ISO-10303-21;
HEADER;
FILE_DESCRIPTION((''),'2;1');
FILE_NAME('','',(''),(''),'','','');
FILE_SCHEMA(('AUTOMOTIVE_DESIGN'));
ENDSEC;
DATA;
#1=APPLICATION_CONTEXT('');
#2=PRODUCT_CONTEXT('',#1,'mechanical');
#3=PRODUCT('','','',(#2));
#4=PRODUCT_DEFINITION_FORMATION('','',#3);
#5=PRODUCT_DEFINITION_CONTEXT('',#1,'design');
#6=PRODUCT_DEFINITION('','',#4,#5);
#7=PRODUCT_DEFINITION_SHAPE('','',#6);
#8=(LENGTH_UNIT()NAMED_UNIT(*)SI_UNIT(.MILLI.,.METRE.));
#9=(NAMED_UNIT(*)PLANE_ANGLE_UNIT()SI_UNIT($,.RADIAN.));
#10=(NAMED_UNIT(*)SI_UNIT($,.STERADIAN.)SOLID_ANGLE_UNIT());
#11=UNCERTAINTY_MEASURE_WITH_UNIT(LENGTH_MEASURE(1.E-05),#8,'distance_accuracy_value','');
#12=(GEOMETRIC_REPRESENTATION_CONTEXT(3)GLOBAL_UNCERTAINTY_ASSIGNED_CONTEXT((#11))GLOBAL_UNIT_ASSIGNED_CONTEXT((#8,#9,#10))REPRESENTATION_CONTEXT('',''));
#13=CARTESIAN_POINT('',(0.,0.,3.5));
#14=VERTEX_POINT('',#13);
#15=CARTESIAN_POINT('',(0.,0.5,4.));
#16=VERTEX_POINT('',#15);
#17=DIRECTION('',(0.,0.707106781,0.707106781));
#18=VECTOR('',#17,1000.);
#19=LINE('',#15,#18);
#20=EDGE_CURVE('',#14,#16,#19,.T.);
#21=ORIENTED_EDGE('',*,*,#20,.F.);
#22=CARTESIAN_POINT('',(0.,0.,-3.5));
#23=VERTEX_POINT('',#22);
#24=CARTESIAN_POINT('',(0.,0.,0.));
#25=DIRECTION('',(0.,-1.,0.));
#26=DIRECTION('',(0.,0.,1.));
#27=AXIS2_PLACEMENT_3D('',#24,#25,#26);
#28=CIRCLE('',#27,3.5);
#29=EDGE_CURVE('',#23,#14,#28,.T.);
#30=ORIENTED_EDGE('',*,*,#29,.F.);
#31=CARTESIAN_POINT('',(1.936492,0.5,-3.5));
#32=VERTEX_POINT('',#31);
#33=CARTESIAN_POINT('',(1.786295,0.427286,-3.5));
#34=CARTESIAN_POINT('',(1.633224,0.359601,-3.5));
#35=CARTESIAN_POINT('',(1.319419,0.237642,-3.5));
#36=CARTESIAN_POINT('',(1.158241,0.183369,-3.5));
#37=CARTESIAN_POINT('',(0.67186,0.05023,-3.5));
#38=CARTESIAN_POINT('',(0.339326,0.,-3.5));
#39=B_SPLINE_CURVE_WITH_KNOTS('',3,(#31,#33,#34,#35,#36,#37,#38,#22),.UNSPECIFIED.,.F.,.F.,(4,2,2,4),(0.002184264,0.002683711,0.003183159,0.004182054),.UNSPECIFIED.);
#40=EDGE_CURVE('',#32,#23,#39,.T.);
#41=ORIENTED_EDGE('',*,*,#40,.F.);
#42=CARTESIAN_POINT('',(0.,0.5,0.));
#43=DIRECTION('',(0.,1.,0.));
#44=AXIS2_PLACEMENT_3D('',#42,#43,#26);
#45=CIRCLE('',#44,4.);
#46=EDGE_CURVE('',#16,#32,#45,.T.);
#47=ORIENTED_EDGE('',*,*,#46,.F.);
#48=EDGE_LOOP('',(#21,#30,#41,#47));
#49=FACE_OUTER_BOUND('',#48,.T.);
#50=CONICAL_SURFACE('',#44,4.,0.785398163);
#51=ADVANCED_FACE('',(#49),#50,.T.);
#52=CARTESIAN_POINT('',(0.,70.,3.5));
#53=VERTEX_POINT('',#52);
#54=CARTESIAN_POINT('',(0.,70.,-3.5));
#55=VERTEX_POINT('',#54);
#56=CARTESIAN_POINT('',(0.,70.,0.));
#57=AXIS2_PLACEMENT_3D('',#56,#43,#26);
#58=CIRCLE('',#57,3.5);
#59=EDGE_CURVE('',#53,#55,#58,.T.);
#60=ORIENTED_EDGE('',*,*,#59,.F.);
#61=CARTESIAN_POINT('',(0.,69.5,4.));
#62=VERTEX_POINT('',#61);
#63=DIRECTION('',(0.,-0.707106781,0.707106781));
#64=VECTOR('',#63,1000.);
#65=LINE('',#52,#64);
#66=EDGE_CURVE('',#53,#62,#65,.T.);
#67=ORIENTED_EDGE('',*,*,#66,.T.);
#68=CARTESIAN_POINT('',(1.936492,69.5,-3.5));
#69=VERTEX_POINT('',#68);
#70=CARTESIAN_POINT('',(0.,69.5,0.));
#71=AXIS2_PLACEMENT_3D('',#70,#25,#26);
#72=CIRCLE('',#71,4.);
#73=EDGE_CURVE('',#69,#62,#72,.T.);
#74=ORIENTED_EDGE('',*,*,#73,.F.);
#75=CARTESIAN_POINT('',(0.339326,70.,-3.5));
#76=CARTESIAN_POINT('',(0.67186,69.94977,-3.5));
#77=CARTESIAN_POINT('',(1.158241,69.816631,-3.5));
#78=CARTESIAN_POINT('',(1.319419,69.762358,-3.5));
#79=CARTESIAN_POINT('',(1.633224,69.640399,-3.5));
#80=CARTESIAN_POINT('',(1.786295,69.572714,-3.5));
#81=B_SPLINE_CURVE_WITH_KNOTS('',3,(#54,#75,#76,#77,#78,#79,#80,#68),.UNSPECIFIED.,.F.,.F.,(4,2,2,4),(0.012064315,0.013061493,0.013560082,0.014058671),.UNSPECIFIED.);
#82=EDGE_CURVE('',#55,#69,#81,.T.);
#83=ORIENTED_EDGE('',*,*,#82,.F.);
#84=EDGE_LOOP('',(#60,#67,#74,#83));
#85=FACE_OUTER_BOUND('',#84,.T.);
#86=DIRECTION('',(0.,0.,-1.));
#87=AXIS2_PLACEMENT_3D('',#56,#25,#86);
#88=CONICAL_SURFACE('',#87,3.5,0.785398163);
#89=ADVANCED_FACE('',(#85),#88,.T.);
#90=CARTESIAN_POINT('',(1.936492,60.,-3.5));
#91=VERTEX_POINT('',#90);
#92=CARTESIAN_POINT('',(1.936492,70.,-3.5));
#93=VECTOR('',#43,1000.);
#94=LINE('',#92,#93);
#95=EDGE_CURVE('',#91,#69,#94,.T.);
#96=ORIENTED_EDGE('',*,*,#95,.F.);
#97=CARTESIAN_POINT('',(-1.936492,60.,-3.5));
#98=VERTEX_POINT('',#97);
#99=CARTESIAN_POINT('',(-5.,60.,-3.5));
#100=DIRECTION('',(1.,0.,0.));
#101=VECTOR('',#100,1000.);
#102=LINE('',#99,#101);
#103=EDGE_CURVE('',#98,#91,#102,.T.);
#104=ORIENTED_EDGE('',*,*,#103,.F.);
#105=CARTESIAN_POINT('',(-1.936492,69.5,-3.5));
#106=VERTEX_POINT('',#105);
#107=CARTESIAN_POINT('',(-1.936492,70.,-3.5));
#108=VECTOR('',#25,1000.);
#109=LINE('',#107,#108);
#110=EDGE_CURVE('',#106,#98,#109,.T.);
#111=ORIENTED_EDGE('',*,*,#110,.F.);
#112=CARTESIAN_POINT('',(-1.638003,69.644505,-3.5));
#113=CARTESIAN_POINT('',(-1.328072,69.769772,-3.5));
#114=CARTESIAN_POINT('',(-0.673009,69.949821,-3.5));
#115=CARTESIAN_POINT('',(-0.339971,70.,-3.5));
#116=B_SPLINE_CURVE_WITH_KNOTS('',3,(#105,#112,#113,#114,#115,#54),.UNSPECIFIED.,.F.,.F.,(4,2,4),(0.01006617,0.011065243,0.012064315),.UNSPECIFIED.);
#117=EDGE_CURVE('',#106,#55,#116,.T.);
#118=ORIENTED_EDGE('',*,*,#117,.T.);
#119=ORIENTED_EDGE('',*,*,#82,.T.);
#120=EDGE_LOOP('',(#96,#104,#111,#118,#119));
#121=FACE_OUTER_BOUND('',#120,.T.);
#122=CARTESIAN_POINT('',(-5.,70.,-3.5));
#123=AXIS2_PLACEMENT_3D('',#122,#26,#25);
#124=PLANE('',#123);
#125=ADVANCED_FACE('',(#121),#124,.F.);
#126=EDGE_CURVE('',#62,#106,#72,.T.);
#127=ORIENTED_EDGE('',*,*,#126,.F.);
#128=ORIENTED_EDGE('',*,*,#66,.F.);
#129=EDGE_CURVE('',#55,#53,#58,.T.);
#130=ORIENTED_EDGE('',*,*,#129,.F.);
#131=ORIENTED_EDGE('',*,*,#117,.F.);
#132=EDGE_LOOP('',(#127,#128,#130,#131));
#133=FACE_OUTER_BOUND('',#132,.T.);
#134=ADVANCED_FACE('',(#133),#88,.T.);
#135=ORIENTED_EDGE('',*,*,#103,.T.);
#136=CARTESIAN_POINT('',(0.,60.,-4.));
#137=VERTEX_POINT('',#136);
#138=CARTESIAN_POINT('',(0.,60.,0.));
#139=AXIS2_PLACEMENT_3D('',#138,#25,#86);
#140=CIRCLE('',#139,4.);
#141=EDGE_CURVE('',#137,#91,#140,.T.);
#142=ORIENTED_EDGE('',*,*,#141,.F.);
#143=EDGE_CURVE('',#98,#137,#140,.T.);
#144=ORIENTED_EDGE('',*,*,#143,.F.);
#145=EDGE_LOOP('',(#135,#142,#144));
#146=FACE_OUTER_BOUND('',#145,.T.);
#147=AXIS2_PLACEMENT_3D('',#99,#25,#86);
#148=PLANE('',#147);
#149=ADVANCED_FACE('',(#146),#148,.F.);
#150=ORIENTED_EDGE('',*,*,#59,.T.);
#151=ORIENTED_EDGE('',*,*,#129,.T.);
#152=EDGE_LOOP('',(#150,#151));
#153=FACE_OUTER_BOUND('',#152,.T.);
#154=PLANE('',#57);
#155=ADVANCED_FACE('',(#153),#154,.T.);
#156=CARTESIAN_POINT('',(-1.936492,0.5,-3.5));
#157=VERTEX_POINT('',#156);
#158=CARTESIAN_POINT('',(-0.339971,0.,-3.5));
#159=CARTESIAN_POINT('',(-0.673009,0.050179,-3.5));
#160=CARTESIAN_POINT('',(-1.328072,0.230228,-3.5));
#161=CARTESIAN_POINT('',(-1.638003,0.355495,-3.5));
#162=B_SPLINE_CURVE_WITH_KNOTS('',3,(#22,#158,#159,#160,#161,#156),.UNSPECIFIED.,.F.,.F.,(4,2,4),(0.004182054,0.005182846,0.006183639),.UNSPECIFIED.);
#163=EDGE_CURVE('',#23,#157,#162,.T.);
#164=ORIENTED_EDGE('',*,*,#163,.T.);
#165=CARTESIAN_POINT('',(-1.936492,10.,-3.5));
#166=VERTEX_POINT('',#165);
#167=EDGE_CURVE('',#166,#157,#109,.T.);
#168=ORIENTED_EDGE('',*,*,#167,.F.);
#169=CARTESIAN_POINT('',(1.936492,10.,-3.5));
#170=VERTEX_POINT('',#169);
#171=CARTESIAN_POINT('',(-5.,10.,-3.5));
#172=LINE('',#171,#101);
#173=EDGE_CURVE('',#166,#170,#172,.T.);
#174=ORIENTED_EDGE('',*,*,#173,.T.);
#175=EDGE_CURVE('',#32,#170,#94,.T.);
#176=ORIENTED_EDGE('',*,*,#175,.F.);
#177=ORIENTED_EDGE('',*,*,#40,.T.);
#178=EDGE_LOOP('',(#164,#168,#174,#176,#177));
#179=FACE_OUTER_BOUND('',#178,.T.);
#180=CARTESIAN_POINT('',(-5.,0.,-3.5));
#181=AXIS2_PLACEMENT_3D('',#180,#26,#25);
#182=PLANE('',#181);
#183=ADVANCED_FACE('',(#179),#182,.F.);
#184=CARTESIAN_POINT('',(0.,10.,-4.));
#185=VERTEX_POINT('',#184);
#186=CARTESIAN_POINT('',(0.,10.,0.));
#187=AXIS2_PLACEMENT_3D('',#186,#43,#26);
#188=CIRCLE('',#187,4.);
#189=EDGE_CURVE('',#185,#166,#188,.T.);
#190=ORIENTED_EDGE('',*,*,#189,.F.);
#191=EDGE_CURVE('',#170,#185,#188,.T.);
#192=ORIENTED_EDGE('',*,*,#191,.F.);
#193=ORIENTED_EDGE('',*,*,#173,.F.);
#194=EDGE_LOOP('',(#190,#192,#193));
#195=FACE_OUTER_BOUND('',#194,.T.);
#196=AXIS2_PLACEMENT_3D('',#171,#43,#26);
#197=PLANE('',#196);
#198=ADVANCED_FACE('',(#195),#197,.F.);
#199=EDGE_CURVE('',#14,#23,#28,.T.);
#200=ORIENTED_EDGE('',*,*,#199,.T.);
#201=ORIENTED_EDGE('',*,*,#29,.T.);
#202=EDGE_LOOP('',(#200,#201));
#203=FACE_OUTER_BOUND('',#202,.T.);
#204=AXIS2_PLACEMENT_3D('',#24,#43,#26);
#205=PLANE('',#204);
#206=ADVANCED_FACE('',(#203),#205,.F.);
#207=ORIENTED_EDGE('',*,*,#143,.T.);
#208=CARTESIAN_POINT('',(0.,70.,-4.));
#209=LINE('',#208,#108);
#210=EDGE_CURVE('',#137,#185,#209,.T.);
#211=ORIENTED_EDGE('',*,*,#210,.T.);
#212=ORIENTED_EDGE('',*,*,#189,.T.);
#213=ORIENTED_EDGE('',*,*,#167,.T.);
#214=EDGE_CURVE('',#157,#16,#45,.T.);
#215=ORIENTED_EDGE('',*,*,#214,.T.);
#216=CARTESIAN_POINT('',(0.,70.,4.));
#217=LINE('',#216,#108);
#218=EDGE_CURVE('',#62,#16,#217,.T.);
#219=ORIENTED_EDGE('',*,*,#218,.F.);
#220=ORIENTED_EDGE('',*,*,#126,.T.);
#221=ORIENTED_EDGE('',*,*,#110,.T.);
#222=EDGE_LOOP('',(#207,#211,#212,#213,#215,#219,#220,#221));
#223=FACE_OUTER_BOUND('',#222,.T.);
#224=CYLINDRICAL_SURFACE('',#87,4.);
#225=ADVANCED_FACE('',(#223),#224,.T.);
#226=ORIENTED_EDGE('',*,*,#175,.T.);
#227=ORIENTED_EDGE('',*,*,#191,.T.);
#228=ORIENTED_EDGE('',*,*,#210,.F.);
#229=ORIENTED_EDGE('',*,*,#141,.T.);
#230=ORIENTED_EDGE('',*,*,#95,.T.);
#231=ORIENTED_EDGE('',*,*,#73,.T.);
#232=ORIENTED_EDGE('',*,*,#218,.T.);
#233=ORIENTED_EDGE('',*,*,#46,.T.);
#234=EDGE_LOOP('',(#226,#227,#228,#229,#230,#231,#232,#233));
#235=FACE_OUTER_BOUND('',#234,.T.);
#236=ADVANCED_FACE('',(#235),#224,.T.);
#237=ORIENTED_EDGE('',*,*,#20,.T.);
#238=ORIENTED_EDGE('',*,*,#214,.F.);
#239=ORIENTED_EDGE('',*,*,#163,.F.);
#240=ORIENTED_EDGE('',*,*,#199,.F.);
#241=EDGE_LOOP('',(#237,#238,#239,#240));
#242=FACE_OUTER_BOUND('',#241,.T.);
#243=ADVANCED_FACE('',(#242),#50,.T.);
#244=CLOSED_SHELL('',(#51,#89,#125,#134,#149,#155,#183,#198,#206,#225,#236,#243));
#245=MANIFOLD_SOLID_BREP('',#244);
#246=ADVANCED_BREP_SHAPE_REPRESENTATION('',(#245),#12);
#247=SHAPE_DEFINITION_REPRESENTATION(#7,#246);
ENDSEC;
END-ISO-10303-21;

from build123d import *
from build123d.topology import SkipClean

# Parameters (mm, degrees)
SKETCH1_R           = 4
BOSS_EXTRUDE1_DEPTH = 70
CHAMFER1_SIZE       = 0.5
SKETCH2_W           = 1.564608121
SKETCH2_H           = 10
CUT_EXTRUDE1_DEPTH  = 5


with BuildPart() as part:
    # Sketch1 → Boss-Extrude1 (new body)
    with BuildSketch(Plane(origin=(0, 0, 0), x_dir=(1, 0, 0), z_dir=(0, 1, 0))):
        with Locations(Location((0, 0, 0), (0, 0, 270))):
            Circle(SKETCH1_R)
    extrude(amount=BOSS_EXTRUDE1_DEPTH)

    # Chamfer1
    chamfer1_edges = [part.edges().sort_by_distance(p)[0] for p in [
        (0, 0, -4),
        (0, 70, -4),
    ]]
    chamfer(chamfer1_edges, length=CHAMFER1_SIZE)

    # Sketch2 → Cut-Extrude1 (cut, symmetric)
    with SkipClean():  # the faces are left unmerged after this step: merging them gives an invalid solid
        with BuildSketch(Plane(origin=(0, 0, 0), x_dir=(0, 0, -1), z_dir=(1, 0, 0))):
            with Locations((4.28230406, 65)):
                Rectangle(SKETCH2_W, SKETCH2_H)
            with Locations((4.28230406, 5)):
                Rectangle(SKETCH2_W, SKETCH2_H)
        extrude(amount=CUT_EXTRUDE1_DEPTH, both=True, mode=Mode.SUBTRACT)


solid = part.part
